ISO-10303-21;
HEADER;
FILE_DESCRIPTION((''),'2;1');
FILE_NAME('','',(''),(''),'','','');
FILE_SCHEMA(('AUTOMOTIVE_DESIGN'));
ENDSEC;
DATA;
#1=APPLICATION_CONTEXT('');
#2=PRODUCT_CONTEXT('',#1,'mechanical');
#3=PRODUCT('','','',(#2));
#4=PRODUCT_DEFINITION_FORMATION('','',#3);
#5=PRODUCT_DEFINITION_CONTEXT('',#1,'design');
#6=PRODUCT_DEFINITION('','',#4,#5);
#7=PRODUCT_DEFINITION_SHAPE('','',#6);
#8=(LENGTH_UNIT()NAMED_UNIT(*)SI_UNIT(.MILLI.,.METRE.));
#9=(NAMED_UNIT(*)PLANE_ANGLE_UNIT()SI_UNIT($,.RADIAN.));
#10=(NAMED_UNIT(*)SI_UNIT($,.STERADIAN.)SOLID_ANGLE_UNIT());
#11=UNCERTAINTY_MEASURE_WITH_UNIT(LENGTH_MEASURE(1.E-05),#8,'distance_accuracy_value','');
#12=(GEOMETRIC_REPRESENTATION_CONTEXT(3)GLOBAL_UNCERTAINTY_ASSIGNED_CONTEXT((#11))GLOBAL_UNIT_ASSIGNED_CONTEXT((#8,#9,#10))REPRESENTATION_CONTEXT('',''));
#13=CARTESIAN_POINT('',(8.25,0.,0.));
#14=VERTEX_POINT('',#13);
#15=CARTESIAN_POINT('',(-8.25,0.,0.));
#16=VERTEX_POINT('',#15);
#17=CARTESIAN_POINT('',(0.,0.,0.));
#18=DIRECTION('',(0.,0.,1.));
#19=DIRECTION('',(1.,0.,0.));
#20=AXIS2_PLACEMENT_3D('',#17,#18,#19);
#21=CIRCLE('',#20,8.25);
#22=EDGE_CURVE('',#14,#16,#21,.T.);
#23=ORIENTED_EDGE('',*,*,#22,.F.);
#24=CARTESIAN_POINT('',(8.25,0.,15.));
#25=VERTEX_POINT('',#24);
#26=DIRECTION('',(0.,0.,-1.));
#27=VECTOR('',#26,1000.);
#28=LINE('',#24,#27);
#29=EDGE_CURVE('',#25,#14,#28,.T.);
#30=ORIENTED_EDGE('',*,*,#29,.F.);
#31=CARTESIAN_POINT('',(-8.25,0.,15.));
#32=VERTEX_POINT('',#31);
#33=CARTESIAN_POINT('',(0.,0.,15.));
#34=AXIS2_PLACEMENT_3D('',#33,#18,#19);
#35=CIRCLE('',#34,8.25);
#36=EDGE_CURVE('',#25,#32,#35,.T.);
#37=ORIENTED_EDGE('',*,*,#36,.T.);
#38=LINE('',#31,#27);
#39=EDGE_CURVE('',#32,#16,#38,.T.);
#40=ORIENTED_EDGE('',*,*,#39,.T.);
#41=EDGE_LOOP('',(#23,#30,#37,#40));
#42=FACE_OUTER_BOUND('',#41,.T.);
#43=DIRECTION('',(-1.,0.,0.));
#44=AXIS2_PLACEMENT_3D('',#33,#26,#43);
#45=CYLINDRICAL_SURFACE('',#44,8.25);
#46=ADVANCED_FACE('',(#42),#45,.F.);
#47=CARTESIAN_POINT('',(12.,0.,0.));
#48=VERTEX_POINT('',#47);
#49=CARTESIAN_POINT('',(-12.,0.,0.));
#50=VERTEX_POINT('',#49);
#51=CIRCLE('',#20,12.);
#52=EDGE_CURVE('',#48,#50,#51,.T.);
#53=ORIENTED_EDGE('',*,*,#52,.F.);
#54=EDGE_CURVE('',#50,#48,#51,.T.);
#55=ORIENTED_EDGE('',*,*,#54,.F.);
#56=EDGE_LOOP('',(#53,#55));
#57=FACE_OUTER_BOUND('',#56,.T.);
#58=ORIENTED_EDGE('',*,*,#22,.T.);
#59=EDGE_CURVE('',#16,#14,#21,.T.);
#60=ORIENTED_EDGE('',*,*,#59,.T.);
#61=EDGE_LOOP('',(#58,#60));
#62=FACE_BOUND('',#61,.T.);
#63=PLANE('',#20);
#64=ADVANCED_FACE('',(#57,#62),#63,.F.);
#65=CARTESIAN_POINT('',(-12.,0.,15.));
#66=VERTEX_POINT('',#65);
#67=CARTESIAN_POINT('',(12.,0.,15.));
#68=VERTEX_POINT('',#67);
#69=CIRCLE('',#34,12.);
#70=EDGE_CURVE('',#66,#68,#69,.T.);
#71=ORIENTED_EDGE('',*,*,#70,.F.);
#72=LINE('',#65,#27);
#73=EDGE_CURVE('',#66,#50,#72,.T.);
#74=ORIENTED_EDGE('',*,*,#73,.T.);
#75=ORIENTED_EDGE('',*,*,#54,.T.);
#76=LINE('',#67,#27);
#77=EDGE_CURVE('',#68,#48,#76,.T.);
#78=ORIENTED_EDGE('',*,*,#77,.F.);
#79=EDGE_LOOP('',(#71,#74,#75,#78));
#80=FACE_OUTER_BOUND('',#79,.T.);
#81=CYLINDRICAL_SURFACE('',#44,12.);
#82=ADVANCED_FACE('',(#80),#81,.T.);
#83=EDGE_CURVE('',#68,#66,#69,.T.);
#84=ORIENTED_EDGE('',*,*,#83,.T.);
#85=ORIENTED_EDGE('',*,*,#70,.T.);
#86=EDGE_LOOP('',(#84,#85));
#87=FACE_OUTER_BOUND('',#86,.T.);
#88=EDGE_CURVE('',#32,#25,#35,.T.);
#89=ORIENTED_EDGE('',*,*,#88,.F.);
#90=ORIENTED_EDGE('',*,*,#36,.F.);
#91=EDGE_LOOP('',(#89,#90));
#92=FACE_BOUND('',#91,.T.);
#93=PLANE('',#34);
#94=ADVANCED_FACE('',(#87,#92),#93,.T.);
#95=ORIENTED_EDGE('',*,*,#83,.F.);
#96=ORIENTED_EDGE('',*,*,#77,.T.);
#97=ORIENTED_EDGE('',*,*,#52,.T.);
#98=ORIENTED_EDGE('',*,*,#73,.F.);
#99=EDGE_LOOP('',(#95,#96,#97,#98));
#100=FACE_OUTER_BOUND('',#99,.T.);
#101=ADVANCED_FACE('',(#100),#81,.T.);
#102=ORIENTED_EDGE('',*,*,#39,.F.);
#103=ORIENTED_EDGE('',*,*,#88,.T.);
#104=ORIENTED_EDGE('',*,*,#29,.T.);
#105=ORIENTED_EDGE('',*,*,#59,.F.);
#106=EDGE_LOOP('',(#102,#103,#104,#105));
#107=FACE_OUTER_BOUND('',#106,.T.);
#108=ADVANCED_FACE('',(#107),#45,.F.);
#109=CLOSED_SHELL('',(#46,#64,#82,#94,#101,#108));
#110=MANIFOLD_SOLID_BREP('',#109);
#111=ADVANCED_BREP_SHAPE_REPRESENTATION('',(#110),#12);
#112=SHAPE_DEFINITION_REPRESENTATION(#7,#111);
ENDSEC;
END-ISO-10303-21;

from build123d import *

# Parameters (mm, degrees)
SKETCH_1_R      = 12
SKETCH_1_R_2    = 8.25
EXTRUDE_1_DEPTH = 15


with BuildPart() as part:
    # 草图1 → 凸台-拉伸1 (new body)
    with BuildSketch(Plane.XY):
        Circle(SKETCH_1_R)
        Circle(SKETCH_1_R_2, mode=Mode.SUBTRACT)
    extrude(amount=EXTRUDE_1_DEPTH)


solid = part.part
